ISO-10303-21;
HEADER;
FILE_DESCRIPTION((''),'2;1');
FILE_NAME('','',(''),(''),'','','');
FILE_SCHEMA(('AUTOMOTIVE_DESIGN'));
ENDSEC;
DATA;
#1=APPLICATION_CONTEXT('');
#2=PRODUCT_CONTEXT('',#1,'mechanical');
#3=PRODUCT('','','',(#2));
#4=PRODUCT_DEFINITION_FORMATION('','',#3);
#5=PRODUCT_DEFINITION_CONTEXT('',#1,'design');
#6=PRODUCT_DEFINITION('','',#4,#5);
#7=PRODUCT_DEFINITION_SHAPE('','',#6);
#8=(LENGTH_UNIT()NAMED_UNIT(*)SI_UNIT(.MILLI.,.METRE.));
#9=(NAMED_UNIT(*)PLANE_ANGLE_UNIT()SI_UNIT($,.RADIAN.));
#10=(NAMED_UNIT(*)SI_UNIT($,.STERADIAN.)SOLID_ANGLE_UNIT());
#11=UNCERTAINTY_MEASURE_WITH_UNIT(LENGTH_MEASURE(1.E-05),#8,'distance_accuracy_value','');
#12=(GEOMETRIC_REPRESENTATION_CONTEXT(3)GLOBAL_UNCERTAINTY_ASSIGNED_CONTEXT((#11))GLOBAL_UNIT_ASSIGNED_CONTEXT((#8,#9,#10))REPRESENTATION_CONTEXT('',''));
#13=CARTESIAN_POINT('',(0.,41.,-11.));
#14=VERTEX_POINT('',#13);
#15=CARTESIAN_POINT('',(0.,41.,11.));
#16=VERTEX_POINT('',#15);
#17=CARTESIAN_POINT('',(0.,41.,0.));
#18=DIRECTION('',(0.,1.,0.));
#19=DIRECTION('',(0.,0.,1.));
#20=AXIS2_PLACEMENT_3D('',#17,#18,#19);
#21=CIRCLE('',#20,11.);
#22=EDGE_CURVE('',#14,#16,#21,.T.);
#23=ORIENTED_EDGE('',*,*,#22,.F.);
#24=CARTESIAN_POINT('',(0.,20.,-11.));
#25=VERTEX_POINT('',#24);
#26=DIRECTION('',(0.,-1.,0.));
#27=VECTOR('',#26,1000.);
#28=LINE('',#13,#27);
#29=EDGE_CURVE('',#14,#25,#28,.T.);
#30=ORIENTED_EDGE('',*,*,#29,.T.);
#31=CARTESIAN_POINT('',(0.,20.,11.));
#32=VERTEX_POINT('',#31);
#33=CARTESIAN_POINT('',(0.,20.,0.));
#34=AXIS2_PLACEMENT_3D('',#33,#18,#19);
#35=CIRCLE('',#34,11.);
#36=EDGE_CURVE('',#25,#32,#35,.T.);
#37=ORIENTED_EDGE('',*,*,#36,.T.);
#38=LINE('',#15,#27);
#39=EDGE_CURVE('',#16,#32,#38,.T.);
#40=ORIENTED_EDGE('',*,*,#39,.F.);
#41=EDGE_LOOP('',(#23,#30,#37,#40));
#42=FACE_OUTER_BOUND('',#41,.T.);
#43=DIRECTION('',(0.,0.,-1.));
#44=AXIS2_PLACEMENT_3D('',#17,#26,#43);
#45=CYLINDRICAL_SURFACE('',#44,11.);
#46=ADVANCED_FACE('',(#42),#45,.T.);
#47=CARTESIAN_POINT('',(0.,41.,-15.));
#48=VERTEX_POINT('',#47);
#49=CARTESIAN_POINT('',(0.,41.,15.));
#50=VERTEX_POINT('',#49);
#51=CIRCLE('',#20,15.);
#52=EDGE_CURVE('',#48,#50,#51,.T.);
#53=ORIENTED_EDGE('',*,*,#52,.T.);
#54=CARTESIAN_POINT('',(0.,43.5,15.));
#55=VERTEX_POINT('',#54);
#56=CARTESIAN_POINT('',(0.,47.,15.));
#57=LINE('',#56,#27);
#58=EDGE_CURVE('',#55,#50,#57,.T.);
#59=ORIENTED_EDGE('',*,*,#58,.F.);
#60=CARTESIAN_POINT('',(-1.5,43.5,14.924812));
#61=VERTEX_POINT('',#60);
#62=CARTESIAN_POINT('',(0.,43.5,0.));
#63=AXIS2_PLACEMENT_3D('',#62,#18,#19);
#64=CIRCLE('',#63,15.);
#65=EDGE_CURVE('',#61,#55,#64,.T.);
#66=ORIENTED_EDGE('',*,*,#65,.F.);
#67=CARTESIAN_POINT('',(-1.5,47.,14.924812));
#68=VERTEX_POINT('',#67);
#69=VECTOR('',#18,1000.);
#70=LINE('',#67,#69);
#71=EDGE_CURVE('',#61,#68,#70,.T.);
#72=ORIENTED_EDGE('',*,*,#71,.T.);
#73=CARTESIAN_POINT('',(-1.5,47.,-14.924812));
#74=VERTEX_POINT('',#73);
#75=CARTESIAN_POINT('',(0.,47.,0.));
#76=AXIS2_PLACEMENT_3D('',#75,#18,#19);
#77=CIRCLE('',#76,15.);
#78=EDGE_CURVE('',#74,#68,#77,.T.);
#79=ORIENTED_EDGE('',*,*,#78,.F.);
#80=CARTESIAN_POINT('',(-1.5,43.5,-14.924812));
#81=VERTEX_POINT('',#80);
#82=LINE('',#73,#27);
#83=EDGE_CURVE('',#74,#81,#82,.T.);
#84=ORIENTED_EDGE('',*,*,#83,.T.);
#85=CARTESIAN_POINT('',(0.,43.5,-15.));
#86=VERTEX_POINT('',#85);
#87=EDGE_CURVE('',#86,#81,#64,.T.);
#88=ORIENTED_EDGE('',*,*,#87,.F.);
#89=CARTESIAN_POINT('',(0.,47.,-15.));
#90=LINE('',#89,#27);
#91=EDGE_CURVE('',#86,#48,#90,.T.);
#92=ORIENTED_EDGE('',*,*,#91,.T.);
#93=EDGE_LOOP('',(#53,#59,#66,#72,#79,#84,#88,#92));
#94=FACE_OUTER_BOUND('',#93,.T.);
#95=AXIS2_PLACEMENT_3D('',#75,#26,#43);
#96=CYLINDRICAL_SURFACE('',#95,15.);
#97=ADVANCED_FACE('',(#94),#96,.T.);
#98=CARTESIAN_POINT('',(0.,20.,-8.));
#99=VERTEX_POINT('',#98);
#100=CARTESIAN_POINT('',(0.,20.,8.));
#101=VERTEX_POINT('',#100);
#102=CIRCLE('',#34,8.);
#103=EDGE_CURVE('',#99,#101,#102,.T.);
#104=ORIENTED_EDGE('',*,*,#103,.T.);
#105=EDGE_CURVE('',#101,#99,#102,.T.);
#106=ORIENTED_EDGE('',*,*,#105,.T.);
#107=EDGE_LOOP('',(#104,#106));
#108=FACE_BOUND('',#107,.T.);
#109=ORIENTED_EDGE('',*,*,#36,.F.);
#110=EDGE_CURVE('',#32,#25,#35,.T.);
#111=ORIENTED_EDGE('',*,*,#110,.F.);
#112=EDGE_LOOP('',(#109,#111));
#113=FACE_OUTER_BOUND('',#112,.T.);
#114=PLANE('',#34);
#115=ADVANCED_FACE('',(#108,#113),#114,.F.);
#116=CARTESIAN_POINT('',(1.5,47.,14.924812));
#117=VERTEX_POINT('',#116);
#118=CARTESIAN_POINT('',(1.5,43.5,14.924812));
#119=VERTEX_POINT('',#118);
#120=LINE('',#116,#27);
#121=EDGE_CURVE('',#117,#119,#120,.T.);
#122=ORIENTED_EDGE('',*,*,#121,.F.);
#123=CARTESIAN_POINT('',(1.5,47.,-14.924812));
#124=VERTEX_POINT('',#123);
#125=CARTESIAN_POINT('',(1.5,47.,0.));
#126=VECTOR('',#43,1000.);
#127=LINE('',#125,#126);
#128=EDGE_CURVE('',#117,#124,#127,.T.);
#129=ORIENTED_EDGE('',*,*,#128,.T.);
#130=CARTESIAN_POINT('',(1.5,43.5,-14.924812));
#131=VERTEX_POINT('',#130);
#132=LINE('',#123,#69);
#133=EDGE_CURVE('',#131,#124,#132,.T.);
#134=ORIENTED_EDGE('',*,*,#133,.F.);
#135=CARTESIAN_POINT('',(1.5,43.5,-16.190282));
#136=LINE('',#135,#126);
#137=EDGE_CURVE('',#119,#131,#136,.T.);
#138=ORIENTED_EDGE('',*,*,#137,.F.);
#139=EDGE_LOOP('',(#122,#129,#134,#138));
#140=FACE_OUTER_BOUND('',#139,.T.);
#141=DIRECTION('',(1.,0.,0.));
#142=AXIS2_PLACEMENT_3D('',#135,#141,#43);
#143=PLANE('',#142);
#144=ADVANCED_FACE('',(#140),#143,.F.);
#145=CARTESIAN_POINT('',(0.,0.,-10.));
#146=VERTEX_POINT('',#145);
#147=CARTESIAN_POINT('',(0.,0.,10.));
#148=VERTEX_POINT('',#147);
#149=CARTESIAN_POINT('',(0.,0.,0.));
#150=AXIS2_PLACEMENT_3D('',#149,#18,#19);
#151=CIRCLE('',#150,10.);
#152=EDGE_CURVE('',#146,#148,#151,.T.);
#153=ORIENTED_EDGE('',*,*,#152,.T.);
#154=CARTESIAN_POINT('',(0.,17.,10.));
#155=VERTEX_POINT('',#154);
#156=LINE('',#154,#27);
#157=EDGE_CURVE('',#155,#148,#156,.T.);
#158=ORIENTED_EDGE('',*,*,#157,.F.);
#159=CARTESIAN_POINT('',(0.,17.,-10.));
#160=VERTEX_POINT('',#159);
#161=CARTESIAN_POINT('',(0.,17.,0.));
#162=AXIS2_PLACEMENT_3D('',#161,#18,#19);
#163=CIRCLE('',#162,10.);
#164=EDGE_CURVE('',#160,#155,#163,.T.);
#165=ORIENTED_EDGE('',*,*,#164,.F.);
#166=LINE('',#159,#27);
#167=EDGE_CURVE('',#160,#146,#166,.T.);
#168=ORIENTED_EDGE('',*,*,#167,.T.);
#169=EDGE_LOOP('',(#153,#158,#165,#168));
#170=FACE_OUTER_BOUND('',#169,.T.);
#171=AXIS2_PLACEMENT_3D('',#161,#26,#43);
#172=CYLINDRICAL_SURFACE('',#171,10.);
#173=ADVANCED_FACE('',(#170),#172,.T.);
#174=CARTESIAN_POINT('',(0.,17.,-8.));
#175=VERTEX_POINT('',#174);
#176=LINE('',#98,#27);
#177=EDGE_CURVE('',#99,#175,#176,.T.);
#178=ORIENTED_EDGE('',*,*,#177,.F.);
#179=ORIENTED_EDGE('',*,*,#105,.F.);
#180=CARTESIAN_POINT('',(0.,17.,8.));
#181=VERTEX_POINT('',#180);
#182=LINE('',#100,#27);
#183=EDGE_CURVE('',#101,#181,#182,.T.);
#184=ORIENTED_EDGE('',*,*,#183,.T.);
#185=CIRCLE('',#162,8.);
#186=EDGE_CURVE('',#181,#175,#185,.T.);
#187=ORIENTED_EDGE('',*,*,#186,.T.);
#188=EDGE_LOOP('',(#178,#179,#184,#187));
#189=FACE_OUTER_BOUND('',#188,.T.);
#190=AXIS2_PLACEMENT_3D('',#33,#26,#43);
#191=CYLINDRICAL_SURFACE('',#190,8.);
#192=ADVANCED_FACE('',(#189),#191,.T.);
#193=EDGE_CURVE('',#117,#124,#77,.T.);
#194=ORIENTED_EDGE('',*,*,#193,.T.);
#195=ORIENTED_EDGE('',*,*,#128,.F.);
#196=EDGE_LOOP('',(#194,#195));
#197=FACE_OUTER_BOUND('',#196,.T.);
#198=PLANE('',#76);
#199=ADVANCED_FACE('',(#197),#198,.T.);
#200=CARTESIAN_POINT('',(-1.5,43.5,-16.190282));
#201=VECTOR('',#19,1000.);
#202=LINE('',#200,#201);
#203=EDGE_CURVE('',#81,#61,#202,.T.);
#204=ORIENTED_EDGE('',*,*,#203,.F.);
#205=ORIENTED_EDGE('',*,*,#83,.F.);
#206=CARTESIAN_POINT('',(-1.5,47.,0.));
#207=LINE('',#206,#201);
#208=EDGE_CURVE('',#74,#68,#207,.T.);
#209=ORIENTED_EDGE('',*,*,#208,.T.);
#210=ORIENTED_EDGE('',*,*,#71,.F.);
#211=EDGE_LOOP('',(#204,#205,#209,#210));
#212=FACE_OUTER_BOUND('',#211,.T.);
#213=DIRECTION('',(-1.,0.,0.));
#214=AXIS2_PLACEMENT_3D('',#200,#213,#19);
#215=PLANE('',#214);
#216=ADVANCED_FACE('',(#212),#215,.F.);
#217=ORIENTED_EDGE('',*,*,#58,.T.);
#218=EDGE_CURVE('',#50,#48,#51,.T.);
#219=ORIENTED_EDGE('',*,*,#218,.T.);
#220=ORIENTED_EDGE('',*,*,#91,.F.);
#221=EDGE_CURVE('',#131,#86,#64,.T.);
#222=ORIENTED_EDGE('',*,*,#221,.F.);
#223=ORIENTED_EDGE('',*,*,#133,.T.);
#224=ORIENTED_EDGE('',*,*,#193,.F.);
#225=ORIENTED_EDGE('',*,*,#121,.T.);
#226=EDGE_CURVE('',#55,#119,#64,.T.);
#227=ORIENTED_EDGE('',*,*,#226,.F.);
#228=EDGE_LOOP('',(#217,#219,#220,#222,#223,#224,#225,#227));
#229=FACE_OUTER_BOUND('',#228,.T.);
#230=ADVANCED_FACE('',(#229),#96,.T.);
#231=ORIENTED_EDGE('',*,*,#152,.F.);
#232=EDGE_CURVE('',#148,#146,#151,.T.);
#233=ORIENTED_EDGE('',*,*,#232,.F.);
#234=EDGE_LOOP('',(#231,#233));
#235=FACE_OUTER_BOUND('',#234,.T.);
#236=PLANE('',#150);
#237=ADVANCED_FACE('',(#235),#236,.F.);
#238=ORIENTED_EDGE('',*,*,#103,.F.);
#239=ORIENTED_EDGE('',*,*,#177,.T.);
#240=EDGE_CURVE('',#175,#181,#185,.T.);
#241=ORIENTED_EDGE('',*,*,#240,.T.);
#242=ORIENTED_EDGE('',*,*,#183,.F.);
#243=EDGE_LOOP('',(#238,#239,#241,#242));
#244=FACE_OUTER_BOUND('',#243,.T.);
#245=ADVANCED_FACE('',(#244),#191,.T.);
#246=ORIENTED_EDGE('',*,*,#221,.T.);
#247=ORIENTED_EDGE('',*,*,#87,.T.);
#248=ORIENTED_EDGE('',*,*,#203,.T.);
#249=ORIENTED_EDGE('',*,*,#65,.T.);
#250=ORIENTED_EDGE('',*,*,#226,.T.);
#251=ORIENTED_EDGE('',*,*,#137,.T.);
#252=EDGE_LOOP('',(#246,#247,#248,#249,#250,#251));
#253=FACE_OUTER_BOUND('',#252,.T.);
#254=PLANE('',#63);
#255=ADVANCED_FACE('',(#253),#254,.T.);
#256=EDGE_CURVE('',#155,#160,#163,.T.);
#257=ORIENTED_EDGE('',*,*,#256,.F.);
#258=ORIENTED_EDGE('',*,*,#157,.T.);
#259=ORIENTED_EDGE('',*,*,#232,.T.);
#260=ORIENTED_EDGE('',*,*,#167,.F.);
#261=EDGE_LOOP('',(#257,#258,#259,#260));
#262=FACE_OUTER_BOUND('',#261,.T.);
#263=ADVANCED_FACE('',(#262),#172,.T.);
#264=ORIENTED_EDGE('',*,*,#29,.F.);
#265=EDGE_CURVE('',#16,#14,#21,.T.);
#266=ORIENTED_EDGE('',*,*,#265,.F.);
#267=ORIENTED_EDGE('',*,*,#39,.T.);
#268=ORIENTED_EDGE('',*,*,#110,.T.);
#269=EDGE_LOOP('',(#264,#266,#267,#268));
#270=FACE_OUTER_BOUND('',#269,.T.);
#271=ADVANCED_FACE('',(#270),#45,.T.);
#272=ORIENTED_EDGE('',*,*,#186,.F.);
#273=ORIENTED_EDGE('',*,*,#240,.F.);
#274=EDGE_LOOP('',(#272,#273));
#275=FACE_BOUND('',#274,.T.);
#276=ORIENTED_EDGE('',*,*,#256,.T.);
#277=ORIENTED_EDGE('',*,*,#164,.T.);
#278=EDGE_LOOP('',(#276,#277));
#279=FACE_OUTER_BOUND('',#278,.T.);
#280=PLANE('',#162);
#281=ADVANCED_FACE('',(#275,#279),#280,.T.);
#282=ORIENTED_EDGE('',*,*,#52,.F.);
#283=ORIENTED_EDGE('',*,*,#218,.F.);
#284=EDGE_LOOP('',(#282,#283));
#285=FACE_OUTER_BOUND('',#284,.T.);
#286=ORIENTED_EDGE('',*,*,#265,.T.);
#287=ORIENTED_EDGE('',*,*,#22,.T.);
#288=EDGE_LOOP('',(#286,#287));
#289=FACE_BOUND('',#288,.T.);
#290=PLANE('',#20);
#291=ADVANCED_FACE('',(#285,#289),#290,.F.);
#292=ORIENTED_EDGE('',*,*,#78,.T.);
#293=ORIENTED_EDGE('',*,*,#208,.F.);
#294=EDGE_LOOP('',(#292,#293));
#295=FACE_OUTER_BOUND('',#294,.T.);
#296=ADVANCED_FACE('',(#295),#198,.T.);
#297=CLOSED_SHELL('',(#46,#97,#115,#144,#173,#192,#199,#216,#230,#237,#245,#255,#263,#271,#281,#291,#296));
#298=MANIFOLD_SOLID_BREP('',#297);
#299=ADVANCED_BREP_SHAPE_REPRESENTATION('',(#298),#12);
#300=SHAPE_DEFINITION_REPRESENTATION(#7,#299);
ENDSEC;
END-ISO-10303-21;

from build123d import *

# Parameters (mm, degrees)
LOWER_SHANK_SKETCH_20_R      = 10
LOWER_SHANK_20_DEPTH         = 17
GROOVE_NECK_SKETCH_16_R      = 8
GROOVE_NECK_16_DEPTH         = 3
UPPER_SHANK_SKETCH_22_R      = 11
UPPER_SHANK_22_DEPTH         = 21
HEAD_SKETCH_30_R             = 15
HEAD_30_DEPTH                = 6
SCREWDRIVER_SLOT_SKETCH_W    = 3
SCREWDRIVER_SLOT_SKETCH_H    = 32.46327366
SCREWDRIVER_SLOT_3X3_5_DEPTH = 3.5


with BuildPart() as part:
    # Lower Shank Sketch Ø20 → Lower Shank Ø20 (new body)
    with BuildSketch(Plane(origin=(0, 0, 0), x_dir=(1, 0, 0), z_dir=(0, 1, 0))):
        with Locations(Location((0, 0, 0), (0, 0, 270))):
            Circle(LOWER_SHANK_SKETCH_20_R)
    extrude(amount=LOWER_SHANK_20_DEPTH)

    # Groove Neck Sketch Ø16 → Groove Neck Ø16 (add)
    with BuildSketch(Plane(origin=(0, 17, 0), x_dir=(1, 0, 0), z_dir=(0, 1, 0))):
        with Locations(Location((0, 0, 0), (0, 0, 270))):
            Circle(GROOVE_NECK_SKETCH_16_R)
    extrude(amount=GROOVE_NECK_16_DEPTH)

    # Upper Shank Sketch Ø22 → Upper Shank Ø22 (add)
    with BuildSketch(Plane(origin=(0, 20, 0), x_dir=(1, 0, 0), z_dir=(0, 1, 0))):
        with Locations(Location((0, 0, 0), (0, 0, 90))):
            Circle(UPPER_SHANK_SKETCH_22_R)
    extrude(amount=UPPER_SHANK_22_DEPTH)

    # Head Sketch Ø30 → Head Ø30 (add)
    with BuildSketch(Plane(origin=(0, 41, 0), x_dir=(1, 0, 0), z_dir=(0, 1, 0))):
        with Locations(Location((0, 0, 0), (0, 0, 270))):
            Circle(HEAD_SKETCH_30_R)
    extrude(amount=HEAD_30_DEPTH)

    # Screwdriver Slot Sketch → Screwdriver Slot 3x3.5 (cut)
    with BuildSketch(Plane(origin=(0, 47, 0), x_dir=(1, 0, 0), z_dir=(0, 1, 0))):
        with Locations((0, -0.041354489)):
            Rectangle(SCREWDRIVER_SLOT_SKETCH_W, SCREWDRIVER_SLOT_SKETCH_H)
    extrude(amount=-SCREWDRIVER_SLOT_3X3_5_DEPTH, mode=Mode.SUBTRACT)


solid = part.part
